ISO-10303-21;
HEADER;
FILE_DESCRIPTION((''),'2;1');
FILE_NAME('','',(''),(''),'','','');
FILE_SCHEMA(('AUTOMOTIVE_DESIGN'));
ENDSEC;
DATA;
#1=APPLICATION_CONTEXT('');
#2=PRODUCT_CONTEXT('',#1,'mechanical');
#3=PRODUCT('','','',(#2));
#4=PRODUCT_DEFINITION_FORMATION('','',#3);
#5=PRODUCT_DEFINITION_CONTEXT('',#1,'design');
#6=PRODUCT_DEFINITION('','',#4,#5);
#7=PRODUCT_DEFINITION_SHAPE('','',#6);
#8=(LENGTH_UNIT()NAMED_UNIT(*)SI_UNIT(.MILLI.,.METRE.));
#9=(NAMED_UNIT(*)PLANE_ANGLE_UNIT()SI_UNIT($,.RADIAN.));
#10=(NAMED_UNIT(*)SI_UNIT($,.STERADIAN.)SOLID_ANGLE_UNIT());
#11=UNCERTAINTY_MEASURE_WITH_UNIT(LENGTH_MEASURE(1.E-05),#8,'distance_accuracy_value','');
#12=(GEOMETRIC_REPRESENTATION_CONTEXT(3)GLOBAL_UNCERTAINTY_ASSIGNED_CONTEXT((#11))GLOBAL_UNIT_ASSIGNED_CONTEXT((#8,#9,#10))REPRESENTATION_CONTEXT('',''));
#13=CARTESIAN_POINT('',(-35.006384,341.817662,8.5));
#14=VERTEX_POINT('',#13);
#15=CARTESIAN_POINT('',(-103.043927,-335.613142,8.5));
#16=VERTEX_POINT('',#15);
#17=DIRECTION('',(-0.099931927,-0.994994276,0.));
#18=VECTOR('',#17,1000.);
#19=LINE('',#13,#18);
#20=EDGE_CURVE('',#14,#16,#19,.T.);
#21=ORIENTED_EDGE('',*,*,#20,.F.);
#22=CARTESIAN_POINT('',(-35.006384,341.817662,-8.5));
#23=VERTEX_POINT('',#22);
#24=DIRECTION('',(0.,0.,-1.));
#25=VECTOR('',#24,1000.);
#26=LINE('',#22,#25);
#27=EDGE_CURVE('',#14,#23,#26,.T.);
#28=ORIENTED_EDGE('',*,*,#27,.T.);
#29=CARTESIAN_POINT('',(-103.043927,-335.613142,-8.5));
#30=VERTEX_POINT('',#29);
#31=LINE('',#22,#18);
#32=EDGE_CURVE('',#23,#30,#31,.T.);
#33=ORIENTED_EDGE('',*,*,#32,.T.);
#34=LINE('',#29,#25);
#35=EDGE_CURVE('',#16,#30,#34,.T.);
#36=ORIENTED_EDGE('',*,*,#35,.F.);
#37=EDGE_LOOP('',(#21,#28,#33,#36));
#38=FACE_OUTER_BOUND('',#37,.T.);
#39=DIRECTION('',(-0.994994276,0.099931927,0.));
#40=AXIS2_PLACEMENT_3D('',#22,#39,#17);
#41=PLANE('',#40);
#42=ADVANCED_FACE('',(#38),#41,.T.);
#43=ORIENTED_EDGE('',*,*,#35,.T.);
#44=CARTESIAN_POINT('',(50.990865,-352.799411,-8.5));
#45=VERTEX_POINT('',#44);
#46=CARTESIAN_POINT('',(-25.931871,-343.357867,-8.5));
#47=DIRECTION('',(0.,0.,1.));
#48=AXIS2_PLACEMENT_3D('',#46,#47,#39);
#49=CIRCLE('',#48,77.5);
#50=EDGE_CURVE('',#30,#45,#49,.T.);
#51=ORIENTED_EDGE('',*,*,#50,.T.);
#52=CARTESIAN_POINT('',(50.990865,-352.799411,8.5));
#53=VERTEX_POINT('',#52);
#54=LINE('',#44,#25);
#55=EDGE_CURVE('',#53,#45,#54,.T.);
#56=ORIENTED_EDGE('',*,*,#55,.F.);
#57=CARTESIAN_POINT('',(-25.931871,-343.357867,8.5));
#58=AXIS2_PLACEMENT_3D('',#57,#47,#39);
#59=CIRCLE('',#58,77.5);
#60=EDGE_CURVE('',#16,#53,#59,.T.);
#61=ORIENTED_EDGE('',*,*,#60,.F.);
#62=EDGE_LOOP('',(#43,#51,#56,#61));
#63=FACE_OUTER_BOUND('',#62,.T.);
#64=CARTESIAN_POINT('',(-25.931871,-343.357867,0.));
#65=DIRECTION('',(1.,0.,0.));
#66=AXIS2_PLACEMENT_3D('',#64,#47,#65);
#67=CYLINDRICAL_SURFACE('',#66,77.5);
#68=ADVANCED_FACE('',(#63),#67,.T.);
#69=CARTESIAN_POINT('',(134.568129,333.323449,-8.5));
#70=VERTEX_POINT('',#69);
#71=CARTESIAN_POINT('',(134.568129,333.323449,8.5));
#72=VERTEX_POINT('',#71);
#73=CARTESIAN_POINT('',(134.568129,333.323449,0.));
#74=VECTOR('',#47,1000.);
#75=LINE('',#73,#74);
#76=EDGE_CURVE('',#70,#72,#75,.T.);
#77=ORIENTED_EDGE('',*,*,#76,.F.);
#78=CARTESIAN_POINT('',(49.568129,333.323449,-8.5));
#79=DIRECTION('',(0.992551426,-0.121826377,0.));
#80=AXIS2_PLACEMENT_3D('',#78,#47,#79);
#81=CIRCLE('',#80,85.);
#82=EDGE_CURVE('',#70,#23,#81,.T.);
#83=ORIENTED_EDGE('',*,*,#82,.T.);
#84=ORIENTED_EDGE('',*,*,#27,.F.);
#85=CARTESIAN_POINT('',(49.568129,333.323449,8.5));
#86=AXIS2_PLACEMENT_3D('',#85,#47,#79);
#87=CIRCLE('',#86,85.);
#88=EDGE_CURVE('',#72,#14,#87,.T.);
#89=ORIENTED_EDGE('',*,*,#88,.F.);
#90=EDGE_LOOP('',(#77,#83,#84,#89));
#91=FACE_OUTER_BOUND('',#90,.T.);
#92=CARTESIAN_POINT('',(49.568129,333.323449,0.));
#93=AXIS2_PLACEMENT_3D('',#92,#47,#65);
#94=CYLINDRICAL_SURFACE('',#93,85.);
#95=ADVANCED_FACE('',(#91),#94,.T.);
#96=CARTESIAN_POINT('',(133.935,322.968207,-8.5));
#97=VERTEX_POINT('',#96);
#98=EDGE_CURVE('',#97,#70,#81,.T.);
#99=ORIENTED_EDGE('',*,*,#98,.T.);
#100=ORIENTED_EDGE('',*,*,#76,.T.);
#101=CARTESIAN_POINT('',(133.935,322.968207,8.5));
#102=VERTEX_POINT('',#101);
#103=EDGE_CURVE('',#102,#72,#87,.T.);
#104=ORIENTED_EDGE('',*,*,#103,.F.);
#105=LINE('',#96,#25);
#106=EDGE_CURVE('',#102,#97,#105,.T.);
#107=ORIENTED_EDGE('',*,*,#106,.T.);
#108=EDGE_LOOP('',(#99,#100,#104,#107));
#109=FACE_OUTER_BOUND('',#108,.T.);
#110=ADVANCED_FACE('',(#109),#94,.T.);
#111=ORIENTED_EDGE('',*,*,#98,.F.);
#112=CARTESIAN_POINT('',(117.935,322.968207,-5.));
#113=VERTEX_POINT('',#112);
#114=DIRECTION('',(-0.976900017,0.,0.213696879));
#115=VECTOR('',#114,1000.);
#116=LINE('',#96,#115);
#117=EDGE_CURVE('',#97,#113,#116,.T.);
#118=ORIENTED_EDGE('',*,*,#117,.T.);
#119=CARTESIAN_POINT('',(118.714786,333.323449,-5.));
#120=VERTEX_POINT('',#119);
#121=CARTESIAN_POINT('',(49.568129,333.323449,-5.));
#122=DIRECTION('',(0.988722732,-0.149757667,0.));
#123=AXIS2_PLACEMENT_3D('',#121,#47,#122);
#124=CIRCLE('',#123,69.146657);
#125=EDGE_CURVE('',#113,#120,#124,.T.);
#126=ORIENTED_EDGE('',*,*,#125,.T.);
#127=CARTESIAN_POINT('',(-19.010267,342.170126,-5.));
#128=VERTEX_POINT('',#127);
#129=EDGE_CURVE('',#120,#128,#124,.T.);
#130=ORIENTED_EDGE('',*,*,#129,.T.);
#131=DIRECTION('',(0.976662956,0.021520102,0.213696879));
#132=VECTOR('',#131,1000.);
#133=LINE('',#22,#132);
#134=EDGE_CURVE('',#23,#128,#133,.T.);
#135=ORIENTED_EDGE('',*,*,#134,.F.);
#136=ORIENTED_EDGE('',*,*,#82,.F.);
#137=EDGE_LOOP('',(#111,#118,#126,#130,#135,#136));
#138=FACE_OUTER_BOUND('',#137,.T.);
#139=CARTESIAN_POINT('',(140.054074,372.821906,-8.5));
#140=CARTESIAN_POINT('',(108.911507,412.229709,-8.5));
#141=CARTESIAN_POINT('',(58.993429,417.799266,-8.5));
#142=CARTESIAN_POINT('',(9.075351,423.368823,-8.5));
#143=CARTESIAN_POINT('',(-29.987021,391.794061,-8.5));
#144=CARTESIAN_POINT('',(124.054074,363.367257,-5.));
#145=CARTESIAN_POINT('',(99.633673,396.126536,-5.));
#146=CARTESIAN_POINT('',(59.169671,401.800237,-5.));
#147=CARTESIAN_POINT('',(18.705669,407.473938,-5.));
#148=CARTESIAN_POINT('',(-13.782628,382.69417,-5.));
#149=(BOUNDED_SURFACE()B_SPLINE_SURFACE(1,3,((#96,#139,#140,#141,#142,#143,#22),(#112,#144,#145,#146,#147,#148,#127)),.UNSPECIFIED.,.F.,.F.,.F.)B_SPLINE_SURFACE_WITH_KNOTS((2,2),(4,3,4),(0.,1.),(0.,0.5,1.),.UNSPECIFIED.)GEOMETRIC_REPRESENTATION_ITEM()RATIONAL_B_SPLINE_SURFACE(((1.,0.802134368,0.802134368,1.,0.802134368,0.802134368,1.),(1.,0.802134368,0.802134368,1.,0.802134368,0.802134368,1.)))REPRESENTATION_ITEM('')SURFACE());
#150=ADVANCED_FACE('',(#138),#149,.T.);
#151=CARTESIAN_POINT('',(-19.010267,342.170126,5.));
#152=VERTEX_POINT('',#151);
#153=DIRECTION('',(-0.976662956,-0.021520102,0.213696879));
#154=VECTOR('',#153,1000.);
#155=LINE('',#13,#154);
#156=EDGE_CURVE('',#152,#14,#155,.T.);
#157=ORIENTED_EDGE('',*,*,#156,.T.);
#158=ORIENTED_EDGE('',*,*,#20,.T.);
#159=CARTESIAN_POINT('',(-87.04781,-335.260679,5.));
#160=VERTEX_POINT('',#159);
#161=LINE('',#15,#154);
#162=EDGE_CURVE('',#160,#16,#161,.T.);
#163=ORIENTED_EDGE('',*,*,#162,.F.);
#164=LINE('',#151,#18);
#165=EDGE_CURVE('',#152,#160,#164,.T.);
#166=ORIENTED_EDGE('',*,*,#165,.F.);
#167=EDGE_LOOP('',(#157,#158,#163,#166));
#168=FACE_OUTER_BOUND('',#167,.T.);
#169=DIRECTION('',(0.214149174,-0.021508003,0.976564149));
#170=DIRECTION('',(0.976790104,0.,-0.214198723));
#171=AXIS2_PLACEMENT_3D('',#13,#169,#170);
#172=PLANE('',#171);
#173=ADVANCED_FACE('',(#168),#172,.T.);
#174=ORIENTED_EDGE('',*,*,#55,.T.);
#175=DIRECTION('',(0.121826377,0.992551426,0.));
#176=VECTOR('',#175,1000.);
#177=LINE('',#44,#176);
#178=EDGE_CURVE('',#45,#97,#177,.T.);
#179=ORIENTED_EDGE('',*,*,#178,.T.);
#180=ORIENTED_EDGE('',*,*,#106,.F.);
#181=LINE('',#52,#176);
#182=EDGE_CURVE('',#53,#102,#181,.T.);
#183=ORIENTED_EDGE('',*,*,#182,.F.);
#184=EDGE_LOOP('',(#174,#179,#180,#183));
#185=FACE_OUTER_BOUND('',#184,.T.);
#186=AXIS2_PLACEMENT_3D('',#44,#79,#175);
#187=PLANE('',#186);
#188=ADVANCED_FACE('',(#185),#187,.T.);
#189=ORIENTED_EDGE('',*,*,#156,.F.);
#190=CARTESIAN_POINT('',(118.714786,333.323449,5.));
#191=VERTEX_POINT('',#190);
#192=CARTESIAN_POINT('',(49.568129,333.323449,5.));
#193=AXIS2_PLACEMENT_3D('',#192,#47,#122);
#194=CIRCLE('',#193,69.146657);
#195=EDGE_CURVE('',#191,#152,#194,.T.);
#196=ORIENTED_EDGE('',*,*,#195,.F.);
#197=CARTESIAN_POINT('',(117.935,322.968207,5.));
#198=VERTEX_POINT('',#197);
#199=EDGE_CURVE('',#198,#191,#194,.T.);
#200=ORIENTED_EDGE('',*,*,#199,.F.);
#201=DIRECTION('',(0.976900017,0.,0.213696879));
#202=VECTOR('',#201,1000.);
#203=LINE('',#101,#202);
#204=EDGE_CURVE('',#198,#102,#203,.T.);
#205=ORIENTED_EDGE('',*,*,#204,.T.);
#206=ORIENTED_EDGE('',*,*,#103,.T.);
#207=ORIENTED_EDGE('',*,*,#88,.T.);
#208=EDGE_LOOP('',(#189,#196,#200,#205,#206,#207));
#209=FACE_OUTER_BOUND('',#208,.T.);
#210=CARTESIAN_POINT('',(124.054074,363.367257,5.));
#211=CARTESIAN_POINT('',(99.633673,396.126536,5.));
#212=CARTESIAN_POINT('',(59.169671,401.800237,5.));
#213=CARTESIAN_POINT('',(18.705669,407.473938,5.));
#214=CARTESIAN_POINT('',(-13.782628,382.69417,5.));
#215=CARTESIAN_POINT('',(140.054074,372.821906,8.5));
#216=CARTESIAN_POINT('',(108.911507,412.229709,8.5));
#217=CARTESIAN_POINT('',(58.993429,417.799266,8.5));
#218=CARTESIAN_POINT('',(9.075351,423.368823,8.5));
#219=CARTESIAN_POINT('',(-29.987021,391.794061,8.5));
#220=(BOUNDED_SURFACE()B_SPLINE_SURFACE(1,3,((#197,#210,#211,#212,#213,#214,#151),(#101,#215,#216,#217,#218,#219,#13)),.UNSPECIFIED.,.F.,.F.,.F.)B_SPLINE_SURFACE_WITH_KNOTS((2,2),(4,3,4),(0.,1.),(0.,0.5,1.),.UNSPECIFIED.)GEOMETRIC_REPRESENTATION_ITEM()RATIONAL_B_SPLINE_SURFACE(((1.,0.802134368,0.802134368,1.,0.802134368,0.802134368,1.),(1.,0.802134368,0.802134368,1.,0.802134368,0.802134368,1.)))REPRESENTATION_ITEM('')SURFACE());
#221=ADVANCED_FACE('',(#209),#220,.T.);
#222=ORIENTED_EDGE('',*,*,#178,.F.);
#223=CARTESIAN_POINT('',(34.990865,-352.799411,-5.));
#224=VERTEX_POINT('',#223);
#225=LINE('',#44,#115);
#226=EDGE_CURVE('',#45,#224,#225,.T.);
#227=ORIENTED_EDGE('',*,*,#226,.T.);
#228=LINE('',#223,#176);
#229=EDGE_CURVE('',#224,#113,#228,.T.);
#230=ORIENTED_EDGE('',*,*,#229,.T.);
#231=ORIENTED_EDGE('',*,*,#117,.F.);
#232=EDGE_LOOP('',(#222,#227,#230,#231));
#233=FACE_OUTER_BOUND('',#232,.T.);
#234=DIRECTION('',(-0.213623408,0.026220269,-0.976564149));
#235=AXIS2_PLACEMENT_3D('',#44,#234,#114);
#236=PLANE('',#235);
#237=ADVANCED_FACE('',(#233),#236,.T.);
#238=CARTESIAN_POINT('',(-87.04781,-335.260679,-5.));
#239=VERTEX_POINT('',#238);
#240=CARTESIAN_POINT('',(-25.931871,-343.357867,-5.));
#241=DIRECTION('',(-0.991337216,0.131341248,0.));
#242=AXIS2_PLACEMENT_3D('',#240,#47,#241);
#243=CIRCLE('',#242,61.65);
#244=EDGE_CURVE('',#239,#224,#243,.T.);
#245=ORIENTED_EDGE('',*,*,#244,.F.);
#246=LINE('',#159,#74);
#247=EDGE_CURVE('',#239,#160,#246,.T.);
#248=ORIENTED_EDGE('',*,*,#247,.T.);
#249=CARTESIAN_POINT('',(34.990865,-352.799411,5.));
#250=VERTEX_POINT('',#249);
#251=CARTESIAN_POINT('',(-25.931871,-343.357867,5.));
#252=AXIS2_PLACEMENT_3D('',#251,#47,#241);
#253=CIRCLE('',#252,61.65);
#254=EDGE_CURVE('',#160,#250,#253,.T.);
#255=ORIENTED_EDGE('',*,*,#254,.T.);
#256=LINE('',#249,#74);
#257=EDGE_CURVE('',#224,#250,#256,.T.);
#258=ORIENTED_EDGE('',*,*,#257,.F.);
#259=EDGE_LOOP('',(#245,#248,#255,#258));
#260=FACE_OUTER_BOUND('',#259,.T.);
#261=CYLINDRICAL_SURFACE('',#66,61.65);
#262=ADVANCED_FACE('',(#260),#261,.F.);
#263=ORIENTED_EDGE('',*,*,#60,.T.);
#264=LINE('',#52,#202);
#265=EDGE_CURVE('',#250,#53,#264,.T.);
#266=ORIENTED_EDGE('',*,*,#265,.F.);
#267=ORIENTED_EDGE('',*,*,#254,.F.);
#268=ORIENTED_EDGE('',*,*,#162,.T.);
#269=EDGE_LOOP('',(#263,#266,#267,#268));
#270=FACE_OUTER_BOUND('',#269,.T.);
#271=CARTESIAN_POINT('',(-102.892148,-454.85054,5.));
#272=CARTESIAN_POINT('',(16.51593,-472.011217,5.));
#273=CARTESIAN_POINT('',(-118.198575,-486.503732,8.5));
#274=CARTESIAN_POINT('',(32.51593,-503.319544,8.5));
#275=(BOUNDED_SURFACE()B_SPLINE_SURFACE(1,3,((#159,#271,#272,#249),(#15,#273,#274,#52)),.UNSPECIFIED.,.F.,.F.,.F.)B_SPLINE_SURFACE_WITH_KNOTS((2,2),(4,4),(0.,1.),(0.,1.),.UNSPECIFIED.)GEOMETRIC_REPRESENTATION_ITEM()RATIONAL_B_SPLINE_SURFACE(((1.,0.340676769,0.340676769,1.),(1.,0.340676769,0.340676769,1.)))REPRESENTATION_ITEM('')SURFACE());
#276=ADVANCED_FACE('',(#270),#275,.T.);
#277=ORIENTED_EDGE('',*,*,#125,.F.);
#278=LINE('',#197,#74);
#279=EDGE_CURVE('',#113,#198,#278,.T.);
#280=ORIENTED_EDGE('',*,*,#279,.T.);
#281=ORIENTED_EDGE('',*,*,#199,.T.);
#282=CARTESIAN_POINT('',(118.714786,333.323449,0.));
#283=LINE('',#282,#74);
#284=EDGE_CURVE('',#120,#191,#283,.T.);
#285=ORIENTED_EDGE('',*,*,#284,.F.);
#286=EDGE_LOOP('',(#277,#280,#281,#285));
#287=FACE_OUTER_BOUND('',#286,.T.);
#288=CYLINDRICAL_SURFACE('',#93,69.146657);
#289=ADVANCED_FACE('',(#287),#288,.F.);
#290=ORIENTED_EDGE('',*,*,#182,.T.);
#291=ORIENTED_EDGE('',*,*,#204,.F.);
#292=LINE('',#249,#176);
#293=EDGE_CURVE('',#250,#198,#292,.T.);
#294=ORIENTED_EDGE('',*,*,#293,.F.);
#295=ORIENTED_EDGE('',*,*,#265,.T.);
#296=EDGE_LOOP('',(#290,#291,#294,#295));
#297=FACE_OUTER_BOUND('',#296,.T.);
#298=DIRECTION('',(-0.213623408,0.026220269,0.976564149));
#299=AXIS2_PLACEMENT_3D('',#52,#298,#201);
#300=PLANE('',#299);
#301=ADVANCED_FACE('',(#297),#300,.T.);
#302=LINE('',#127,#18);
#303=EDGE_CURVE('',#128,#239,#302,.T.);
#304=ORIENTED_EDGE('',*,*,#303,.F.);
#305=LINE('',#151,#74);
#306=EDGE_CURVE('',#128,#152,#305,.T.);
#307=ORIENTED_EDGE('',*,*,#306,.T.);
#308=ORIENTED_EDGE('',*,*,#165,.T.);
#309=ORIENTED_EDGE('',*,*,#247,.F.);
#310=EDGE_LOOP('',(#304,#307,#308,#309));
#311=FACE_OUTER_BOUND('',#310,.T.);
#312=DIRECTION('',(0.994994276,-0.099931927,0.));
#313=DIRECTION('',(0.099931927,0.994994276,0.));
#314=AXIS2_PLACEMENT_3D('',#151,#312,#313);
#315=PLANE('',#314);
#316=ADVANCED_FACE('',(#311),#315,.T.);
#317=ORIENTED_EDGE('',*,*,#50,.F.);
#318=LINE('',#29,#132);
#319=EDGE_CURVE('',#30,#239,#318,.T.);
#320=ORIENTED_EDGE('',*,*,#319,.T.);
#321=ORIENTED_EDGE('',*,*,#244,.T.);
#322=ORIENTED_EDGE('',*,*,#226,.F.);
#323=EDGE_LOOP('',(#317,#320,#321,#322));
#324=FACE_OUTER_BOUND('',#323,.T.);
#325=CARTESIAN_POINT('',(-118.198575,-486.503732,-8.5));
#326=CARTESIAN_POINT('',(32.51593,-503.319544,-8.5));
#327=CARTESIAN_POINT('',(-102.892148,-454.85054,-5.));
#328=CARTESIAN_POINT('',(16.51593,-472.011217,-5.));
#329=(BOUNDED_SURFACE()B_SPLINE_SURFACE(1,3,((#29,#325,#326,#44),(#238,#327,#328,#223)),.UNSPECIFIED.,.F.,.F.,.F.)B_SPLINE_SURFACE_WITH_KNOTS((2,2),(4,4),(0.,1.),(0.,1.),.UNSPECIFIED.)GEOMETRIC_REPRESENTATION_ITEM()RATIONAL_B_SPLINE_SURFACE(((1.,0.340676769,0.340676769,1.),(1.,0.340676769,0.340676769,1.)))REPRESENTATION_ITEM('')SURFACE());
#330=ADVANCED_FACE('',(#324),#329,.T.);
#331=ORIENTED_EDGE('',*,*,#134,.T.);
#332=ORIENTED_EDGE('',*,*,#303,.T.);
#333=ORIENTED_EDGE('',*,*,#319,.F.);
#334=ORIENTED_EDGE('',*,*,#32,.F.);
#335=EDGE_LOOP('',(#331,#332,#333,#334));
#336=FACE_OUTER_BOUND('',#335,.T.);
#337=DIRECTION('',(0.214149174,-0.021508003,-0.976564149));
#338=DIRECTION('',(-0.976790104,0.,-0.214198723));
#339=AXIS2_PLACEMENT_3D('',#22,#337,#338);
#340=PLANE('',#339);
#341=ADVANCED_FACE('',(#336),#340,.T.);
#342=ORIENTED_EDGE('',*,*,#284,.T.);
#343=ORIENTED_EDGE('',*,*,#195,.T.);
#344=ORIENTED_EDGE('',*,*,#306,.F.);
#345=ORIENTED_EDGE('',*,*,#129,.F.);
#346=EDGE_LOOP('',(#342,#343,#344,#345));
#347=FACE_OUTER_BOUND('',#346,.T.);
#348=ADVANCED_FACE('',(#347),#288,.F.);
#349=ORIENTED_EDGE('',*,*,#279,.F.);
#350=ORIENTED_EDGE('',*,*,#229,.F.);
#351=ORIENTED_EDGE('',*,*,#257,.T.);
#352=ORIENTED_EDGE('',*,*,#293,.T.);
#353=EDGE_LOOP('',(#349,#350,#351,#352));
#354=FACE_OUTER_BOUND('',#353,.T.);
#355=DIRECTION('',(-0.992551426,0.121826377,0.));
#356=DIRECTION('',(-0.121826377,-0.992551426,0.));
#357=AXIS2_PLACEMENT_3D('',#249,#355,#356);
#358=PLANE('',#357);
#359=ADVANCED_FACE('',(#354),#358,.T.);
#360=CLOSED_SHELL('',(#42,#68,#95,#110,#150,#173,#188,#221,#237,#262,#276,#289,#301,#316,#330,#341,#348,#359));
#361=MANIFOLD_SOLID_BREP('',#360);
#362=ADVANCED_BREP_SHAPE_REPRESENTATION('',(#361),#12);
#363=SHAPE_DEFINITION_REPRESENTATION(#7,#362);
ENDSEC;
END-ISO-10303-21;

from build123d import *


with BuildPart() as part:
    # 扫描1: sweep along a path in 草图1
    with BuildLine(Plane.XY) as sweep_1_path:
        Line((133.935000245, 322.9682066), (50.990864547, -352.799410804))
        ThreePointArc((50.990864547, -352.799410804), (-34.525526627, -420.379935429), (-103.043927412, -335.613142274))
        Line((-103.043927412, -335.613142274), (-35.006384485, 341.817662407))
        ThreePointArc((-35.006384485, 341.817662407), (58.993428728, 417.799266002), (133.935000245, 322.9682066))
    # 草图2 → 扫描1 (sweep)
    with BuildSketch(Plane(origin=(0, 322.9682066, 0), x_dir=(1, 0, 0), z_dir=(0, 1, 0))):
        Polygon((133.935000245, 8.5), (133.935000245, -8.5), (117.935000245, -5), (117.935000245, 5), align=None)
    sweep(path=sweep_1_path.line)


solid = part.part
